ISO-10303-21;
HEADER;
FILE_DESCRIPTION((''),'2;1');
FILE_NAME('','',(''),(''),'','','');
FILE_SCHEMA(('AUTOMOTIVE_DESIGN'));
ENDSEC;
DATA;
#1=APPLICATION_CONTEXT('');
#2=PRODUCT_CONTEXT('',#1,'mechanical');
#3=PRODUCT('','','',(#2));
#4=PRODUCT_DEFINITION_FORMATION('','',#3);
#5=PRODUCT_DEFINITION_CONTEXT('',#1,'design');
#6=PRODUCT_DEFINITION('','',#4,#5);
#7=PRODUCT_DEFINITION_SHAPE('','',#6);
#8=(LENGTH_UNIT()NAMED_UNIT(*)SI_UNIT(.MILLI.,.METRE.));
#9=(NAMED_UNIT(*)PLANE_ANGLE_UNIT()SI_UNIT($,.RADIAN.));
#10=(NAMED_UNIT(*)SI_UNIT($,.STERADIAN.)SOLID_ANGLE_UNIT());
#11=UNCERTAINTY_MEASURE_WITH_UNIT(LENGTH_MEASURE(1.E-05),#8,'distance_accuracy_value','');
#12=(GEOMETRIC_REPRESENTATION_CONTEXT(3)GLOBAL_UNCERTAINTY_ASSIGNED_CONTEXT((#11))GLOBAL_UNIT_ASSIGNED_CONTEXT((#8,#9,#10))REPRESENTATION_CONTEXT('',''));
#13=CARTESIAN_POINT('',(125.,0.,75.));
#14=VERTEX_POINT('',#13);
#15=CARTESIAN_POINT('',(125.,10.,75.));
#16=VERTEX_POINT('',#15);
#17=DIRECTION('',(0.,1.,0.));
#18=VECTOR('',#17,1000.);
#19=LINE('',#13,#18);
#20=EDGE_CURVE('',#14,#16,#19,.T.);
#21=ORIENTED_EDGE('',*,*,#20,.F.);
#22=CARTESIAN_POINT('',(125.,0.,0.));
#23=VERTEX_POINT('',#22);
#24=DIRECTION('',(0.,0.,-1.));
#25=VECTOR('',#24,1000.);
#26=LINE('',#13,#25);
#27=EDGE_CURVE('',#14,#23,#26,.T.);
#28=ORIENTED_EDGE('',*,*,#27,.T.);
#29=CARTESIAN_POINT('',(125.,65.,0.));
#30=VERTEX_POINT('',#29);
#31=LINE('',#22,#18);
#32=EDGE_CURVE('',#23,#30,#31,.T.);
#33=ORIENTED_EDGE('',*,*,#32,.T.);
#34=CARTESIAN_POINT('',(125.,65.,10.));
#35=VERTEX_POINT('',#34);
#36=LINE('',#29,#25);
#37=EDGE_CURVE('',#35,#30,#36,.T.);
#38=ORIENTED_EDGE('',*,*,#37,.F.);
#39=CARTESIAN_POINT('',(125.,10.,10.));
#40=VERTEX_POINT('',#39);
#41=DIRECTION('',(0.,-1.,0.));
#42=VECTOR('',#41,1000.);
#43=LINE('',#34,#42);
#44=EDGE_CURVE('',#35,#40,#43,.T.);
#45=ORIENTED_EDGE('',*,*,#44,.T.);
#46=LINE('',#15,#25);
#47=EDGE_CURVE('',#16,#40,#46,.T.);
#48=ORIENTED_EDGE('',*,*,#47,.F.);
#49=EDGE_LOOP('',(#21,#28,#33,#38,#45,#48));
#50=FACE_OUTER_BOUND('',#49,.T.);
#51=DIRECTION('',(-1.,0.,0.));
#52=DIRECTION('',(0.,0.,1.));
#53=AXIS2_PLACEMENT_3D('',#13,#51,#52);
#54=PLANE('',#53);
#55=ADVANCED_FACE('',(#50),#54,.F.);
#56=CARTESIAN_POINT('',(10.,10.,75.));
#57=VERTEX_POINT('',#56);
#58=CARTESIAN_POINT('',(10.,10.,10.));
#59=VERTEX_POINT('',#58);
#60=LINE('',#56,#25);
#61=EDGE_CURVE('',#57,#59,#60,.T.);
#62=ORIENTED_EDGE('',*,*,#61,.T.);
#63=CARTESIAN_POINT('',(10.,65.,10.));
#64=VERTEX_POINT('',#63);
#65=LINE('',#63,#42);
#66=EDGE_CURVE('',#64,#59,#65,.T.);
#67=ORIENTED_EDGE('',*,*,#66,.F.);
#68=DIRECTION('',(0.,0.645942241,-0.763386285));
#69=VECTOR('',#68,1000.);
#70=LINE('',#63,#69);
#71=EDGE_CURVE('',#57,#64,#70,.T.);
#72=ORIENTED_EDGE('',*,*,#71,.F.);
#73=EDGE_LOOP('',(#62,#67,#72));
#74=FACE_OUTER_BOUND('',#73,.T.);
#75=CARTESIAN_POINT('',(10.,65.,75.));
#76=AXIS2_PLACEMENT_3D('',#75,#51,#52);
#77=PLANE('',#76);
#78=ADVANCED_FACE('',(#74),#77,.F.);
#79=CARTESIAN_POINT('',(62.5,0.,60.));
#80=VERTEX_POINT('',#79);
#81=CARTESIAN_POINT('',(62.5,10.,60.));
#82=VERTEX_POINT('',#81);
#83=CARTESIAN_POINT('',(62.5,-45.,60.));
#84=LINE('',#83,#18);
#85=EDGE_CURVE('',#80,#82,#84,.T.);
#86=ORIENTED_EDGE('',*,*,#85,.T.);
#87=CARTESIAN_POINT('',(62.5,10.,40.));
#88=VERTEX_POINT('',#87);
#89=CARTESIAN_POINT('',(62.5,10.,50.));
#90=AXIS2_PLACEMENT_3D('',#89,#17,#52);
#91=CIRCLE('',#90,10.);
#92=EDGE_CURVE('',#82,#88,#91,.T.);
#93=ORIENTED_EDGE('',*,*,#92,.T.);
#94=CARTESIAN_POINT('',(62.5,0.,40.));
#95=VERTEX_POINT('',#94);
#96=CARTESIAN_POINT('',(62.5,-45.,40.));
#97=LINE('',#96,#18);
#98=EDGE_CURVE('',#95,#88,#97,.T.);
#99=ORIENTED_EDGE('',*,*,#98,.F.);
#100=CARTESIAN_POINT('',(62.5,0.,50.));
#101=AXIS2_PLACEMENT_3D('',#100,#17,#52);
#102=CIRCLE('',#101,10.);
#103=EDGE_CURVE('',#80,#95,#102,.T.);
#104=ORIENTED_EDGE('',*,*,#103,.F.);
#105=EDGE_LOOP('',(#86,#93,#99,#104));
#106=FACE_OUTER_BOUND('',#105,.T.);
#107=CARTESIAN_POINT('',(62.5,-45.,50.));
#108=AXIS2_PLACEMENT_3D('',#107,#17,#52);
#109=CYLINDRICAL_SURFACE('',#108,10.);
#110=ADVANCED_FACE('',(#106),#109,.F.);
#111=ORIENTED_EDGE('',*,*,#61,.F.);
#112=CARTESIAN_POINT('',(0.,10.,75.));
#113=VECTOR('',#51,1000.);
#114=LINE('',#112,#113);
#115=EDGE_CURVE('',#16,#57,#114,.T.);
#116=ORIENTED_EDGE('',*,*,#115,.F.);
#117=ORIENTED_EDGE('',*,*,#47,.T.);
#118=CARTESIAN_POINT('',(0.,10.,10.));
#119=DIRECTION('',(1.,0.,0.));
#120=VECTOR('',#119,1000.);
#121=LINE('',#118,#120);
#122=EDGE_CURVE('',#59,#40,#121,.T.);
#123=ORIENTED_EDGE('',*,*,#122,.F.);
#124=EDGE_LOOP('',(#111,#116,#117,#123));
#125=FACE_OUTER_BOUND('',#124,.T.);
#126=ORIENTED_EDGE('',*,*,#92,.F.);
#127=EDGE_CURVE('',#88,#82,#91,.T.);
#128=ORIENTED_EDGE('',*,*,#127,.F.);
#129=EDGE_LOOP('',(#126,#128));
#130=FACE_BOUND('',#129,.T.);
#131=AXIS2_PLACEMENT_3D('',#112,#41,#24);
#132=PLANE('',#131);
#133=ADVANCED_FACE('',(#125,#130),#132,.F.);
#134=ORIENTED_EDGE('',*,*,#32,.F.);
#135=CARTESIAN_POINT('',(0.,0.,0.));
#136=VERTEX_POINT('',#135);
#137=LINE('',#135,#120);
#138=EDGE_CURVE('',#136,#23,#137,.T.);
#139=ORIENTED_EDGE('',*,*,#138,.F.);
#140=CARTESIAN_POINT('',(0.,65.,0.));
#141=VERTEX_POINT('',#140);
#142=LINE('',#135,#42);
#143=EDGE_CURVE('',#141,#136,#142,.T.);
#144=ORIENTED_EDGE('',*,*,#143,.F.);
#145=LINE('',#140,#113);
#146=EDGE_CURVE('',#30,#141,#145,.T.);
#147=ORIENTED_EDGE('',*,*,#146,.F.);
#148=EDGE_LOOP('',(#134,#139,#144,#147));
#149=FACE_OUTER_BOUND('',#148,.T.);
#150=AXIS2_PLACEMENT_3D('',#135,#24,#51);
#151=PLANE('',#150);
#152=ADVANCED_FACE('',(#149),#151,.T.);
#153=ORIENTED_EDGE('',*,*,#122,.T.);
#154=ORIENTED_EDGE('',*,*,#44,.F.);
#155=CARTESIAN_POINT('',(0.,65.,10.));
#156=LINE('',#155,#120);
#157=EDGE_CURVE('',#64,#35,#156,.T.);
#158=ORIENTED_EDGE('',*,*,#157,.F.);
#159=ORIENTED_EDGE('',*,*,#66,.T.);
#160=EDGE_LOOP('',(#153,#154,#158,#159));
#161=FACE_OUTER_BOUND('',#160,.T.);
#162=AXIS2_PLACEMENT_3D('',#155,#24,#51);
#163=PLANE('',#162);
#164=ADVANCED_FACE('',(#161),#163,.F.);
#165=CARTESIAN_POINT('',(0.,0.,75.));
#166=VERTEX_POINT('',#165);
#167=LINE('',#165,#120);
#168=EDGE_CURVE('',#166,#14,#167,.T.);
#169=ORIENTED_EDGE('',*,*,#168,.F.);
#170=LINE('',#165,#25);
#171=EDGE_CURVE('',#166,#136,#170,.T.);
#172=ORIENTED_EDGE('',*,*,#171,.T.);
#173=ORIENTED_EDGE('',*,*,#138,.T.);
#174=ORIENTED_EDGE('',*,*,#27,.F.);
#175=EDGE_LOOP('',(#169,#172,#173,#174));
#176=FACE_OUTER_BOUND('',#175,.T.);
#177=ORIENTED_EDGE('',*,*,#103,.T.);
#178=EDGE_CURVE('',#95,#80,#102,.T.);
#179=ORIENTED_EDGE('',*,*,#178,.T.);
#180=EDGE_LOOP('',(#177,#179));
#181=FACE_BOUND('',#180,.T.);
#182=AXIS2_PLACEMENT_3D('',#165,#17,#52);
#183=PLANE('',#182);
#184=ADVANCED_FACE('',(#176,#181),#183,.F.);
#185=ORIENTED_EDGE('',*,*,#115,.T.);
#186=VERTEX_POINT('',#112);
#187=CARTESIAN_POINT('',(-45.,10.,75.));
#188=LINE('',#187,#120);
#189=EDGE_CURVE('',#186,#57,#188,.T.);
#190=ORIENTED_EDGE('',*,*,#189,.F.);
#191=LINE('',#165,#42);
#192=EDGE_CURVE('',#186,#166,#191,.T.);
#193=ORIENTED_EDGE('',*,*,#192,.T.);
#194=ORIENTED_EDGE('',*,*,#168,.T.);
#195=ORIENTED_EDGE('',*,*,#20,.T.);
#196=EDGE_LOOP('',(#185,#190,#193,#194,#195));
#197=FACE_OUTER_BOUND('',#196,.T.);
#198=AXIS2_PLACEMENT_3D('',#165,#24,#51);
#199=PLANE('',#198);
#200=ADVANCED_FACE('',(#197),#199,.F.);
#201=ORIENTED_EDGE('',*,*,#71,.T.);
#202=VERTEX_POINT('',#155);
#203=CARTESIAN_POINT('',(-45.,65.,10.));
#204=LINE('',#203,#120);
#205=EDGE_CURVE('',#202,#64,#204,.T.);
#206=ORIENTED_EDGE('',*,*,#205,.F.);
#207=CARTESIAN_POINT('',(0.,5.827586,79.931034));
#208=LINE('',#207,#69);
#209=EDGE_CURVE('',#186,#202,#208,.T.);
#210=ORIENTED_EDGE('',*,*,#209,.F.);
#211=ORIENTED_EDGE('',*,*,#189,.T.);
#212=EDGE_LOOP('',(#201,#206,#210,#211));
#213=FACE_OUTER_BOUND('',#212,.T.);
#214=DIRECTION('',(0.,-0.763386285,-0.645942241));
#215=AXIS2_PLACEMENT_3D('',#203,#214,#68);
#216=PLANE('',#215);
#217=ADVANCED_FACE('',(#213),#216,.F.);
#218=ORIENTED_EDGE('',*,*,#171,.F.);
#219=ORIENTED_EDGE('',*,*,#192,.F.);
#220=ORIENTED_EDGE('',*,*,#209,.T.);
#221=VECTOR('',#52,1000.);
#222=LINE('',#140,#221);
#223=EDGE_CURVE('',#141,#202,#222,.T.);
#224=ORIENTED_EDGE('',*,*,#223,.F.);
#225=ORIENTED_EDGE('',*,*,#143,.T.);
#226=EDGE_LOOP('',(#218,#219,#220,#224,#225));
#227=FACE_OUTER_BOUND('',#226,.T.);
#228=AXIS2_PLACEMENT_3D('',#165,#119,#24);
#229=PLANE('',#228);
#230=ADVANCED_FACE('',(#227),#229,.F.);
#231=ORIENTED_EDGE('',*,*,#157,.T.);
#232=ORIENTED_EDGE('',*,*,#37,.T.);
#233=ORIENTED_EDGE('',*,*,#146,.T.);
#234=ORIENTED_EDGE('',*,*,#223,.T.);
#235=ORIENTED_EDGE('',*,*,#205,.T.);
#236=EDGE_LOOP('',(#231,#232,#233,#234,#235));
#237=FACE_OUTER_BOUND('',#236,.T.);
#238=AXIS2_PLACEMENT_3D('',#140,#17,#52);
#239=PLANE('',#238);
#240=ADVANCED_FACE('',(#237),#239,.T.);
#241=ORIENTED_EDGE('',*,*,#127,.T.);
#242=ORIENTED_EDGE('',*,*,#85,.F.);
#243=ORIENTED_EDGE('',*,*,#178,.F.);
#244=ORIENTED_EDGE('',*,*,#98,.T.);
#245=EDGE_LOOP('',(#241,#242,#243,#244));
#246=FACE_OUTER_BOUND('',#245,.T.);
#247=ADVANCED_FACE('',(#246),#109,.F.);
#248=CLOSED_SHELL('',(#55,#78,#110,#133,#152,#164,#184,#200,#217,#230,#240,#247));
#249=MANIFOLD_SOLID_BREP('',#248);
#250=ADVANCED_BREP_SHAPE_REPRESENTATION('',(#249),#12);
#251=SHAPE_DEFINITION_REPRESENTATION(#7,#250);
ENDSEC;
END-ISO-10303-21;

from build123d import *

# Parameters (mm, degrees)
BASE_PLATE_PROFILE_W  = 125
BASE_PLATE_PROFILE_H  = 10
BASE_PLATE_DEPTH      = 75
BACK_WALL_PROFILE_W   = 125
BACK_WALL_PROFILE_H   = 10
BACK_WALL_DEPTH       = 55
END_WALL_PROFILE_W    = 10
END_WALL_PROFILE_H    = 65
END_WALL_DEPTH        = 55
GUSSET_TRIM_CUT_DEPTH = 55
BASE_HOLE_20_SKETCH_R = 10
BASE_HOLE_20_DEPTH    = 55


with BuildPart() as part:
    # Base Plate Profile → Base Plate (new body)
    with BuildSketch(Plane.XY):
        with Locations((62.5, 5)):
            Rectangle(BASE_PLATE_PROFILE_W, BASE_PLATE_PROFILE_H)
    extrude(amount=BASE_PLATE_DEPTH)

    # Back Wall Profile → Back Wall (add)
    with BuildSketch(Plane(origin=(0, 10, 0), x_dir=(1, 0, 0), z_dir=(0, 1, 0))):
        with Locations((62.5, -5)):
            Rectangle(BACK_WALL_PROFILE_W, BACK_WALL_PROFILE_H)
    extrude(amount=BACK_WALL_DEPTH)

    # End Wall Profile → End Wall (add)
    with BuildSketch(Plane(origin=(0, 10, 0), x_dir=(1, 0, 0), z_dir=(0, 1, 0))):
        with Locations((5, -42.5)):
            Rectangle(END_WALL_PROFILE_W, END_WALL_PROFILE_H)
    extrude(amount=END_WALL_DEPTH)

    # Gusset Trim Profile → Gusset Trim Cut (cut)
    with BuildSketch(Plane(origin=(10, 0, 0), x_dir=(0, 0, -1), z_dir=(1, 0, 0))):
        Polygon((-10, 65), (-75, 10), (-75, 65), align=None)
    extrude(amount=-GUSSET_TRIM_CUT_DEPTH, mode=Mode.SUBTRACT)

    # Base Hole Ø20 Sketch → Base Hole Ø20 (cut)
    with BuildSketch(Plane(origin=(0, 10, 0), x_dir=(1, 0, 0), z_dir=(0, 1, 0))):
        with Locations(Location((62.5, -50, 0), (0, 0, 270))):
            Circle(BASE_HOLE_20_SKETCH_R)
    extrude(amount=-BASE_HOLE_20_DEPTH, mode=Mode.SUBTRACT)


solid = part.part
